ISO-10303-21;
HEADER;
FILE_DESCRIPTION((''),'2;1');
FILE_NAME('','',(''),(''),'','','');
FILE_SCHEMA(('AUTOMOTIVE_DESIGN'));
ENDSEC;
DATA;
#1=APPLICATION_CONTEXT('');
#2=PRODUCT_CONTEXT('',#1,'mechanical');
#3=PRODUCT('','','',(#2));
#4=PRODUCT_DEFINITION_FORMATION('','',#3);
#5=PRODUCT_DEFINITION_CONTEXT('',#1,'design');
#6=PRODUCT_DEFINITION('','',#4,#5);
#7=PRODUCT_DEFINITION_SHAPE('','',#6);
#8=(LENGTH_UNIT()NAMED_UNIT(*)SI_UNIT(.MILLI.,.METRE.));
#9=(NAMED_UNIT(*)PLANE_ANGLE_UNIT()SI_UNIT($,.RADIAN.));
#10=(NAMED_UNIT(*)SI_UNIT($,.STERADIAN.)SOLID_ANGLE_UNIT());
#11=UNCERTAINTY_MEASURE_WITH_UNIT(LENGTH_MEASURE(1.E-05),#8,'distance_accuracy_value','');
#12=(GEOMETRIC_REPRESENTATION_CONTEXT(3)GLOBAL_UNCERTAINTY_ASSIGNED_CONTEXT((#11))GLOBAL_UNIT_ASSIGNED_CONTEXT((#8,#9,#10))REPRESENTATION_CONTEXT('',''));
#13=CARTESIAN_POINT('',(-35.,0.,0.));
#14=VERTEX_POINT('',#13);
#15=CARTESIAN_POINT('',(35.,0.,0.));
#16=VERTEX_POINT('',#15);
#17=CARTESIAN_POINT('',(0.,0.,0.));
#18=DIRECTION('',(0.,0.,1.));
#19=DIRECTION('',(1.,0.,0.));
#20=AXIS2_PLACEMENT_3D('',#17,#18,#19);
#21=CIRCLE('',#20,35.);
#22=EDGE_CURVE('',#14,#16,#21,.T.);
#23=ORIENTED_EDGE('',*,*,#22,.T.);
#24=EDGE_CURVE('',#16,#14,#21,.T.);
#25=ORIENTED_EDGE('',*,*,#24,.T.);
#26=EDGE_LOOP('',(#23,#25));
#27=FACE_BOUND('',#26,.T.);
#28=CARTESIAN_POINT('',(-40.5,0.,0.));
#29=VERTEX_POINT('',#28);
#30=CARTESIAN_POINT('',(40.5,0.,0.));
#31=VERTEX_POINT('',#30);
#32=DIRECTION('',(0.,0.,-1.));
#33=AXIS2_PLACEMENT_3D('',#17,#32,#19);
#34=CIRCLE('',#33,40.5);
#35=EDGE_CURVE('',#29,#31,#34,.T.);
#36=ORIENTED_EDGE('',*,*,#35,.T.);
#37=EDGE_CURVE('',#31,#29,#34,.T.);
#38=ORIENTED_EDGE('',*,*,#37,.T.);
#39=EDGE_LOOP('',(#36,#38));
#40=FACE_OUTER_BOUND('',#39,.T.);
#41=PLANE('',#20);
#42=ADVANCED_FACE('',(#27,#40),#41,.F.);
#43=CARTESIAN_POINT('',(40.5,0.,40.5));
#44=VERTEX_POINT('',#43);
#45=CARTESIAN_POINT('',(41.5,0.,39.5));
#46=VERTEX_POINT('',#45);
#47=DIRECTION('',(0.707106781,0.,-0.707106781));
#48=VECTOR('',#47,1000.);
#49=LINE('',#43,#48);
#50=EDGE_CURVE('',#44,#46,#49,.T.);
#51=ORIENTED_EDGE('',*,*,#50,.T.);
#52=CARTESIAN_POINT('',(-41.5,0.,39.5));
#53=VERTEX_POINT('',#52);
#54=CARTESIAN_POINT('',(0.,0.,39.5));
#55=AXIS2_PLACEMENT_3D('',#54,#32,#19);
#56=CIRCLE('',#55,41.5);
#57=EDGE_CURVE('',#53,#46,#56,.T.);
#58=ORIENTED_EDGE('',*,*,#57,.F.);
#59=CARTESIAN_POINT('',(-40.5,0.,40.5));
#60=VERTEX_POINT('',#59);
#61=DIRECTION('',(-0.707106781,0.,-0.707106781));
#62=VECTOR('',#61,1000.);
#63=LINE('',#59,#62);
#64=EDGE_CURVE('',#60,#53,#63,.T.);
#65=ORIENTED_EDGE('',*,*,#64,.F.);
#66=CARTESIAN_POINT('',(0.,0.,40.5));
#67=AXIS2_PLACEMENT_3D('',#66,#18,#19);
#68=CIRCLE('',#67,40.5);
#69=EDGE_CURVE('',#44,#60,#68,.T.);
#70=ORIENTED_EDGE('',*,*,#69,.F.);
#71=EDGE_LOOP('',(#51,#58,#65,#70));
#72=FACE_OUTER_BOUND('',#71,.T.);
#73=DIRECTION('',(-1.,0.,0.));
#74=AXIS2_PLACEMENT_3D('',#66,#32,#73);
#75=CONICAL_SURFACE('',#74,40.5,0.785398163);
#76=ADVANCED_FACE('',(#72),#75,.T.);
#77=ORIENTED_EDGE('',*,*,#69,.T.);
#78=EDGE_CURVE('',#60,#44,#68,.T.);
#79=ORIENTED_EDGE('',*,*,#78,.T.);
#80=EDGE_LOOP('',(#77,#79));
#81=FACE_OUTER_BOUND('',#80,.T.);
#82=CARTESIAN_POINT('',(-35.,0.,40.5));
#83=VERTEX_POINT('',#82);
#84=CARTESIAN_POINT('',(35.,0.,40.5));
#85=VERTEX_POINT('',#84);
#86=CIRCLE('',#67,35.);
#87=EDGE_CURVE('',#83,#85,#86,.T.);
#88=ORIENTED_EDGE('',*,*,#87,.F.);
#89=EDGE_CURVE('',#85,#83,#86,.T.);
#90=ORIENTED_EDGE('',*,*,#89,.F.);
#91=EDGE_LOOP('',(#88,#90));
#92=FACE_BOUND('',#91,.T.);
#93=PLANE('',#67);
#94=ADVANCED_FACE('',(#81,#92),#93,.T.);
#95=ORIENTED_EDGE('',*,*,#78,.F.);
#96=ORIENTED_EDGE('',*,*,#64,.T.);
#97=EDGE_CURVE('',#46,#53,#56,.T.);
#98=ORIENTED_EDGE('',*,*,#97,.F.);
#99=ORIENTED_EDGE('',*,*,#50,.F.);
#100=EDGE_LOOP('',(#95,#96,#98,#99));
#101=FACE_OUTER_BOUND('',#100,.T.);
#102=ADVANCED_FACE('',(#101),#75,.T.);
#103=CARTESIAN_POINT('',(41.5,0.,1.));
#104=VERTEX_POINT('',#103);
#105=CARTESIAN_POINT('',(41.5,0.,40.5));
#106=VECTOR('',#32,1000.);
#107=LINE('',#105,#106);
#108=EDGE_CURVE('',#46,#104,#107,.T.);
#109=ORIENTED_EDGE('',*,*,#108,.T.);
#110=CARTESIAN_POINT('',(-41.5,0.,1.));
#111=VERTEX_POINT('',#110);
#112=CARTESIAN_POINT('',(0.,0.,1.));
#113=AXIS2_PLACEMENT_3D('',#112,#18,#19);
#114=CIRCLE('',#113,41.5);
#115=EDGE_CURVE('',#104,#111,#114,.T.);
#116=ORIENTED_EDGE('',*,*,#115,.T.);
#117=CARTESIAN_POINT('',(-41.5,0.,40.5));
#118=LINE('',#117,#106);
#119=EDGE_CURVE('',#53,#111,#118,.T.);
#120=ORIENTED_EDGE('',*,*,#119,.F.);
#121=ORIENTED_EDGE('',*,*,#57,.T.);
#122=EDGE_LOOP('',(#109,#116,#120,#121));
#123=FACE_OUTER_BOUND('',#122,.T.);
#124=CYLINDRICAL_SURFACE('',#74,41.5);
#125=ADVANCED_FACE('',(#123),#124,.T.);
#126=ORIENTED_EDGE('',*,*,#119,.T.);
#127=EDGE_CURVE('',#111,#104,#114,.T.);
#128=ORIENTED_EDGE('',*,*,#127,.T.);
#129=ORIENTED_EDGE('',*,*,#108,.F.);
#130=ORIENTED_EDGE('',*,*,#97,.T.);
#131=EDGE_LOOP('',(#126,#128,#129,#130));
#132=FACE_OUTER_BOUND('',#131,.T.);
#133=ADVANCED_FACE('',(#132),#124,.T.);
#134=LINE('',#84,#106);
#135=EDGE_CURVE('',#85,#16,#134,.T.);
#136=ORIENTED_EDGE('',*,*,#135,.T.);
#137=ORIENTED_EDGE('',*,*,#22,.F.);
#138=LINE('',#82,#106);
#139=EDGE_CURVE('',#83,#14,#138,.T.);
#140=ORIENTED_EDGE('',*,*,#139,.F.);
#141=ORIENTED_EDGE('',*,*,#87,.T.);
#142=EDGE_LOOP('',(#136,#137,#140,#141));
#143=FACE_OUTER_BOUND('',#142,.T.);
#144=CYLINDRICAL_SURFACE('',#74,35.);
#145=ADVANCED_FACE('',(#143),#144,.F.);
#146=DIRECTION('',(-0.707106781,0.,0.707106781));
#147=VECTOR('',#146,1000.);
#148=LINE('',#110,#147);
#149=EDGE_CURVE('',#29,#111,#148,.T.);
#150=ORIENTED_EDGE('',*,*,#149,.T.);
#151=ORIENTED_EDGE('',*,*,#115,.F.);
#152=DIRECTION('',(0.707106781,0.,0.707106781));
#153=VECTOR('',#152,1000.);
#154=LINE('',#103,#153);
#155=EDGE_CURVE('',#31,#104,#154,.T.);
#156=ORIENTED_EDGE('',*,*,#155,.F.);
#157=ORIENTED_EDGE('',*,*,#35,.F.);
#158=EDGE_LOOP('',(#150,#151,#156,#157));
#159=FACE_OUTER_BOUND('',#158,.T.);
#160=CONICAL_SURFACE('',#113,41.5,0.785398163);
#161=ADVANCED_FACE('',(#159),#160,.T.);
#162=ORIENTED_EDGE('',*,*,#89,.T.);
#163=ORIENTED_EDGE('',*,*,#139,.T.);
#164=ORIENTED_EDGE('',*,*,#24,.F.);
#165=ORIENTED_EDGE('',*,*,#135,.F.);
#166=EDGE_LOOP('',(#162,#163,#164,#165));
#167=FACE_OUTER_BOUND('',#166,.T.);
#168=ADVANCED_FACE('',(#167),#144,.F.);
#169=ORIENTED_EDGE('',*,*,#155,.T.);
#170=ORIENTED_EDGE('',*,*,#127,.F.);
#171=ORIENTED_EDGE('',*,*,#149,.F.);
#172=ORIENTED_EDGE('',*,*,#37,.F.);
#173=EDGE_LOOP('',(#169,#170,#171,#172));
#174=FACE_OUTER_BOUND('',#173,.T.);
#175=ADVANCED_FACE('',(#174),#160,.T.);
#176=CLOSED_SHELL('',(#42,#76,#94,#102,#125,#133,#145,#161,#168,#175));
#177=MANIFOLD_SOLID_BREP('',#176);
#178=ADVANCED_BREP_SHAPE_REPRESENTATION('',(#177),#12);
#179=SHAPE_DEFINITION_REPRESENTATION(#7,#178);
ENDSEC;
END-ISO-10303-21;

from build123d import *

# Parameters (mm, degrees)
SKETCH1_R      = 41.5
SKETCH1_R_2    = 35
EXTRUDE1_DEPTH = 40.5
CHAMFER1_SIZE  = 1


with BuildPart() as part:
    # Sketch1 → Extrude1 (new body)
    with BuildSketch(Plane.XY):
        Circle(SKETCH1_R)
        Circle(SKETCH1_R_2, mode=Mode.SUBTRACT)
    extrude(amount=EXTRUDE1_DEPTH)

    # Chamfer1
    chamfer1_edges = [part.edges().sort_by_distance(p)[0] for p in [
        (-41.5, 0, 0),
        (-41.5, 0, 40.5),
    ]]
    chamfer(chamfer1_edges, length=CHAMFER1_SIZE)


solid = part.part
